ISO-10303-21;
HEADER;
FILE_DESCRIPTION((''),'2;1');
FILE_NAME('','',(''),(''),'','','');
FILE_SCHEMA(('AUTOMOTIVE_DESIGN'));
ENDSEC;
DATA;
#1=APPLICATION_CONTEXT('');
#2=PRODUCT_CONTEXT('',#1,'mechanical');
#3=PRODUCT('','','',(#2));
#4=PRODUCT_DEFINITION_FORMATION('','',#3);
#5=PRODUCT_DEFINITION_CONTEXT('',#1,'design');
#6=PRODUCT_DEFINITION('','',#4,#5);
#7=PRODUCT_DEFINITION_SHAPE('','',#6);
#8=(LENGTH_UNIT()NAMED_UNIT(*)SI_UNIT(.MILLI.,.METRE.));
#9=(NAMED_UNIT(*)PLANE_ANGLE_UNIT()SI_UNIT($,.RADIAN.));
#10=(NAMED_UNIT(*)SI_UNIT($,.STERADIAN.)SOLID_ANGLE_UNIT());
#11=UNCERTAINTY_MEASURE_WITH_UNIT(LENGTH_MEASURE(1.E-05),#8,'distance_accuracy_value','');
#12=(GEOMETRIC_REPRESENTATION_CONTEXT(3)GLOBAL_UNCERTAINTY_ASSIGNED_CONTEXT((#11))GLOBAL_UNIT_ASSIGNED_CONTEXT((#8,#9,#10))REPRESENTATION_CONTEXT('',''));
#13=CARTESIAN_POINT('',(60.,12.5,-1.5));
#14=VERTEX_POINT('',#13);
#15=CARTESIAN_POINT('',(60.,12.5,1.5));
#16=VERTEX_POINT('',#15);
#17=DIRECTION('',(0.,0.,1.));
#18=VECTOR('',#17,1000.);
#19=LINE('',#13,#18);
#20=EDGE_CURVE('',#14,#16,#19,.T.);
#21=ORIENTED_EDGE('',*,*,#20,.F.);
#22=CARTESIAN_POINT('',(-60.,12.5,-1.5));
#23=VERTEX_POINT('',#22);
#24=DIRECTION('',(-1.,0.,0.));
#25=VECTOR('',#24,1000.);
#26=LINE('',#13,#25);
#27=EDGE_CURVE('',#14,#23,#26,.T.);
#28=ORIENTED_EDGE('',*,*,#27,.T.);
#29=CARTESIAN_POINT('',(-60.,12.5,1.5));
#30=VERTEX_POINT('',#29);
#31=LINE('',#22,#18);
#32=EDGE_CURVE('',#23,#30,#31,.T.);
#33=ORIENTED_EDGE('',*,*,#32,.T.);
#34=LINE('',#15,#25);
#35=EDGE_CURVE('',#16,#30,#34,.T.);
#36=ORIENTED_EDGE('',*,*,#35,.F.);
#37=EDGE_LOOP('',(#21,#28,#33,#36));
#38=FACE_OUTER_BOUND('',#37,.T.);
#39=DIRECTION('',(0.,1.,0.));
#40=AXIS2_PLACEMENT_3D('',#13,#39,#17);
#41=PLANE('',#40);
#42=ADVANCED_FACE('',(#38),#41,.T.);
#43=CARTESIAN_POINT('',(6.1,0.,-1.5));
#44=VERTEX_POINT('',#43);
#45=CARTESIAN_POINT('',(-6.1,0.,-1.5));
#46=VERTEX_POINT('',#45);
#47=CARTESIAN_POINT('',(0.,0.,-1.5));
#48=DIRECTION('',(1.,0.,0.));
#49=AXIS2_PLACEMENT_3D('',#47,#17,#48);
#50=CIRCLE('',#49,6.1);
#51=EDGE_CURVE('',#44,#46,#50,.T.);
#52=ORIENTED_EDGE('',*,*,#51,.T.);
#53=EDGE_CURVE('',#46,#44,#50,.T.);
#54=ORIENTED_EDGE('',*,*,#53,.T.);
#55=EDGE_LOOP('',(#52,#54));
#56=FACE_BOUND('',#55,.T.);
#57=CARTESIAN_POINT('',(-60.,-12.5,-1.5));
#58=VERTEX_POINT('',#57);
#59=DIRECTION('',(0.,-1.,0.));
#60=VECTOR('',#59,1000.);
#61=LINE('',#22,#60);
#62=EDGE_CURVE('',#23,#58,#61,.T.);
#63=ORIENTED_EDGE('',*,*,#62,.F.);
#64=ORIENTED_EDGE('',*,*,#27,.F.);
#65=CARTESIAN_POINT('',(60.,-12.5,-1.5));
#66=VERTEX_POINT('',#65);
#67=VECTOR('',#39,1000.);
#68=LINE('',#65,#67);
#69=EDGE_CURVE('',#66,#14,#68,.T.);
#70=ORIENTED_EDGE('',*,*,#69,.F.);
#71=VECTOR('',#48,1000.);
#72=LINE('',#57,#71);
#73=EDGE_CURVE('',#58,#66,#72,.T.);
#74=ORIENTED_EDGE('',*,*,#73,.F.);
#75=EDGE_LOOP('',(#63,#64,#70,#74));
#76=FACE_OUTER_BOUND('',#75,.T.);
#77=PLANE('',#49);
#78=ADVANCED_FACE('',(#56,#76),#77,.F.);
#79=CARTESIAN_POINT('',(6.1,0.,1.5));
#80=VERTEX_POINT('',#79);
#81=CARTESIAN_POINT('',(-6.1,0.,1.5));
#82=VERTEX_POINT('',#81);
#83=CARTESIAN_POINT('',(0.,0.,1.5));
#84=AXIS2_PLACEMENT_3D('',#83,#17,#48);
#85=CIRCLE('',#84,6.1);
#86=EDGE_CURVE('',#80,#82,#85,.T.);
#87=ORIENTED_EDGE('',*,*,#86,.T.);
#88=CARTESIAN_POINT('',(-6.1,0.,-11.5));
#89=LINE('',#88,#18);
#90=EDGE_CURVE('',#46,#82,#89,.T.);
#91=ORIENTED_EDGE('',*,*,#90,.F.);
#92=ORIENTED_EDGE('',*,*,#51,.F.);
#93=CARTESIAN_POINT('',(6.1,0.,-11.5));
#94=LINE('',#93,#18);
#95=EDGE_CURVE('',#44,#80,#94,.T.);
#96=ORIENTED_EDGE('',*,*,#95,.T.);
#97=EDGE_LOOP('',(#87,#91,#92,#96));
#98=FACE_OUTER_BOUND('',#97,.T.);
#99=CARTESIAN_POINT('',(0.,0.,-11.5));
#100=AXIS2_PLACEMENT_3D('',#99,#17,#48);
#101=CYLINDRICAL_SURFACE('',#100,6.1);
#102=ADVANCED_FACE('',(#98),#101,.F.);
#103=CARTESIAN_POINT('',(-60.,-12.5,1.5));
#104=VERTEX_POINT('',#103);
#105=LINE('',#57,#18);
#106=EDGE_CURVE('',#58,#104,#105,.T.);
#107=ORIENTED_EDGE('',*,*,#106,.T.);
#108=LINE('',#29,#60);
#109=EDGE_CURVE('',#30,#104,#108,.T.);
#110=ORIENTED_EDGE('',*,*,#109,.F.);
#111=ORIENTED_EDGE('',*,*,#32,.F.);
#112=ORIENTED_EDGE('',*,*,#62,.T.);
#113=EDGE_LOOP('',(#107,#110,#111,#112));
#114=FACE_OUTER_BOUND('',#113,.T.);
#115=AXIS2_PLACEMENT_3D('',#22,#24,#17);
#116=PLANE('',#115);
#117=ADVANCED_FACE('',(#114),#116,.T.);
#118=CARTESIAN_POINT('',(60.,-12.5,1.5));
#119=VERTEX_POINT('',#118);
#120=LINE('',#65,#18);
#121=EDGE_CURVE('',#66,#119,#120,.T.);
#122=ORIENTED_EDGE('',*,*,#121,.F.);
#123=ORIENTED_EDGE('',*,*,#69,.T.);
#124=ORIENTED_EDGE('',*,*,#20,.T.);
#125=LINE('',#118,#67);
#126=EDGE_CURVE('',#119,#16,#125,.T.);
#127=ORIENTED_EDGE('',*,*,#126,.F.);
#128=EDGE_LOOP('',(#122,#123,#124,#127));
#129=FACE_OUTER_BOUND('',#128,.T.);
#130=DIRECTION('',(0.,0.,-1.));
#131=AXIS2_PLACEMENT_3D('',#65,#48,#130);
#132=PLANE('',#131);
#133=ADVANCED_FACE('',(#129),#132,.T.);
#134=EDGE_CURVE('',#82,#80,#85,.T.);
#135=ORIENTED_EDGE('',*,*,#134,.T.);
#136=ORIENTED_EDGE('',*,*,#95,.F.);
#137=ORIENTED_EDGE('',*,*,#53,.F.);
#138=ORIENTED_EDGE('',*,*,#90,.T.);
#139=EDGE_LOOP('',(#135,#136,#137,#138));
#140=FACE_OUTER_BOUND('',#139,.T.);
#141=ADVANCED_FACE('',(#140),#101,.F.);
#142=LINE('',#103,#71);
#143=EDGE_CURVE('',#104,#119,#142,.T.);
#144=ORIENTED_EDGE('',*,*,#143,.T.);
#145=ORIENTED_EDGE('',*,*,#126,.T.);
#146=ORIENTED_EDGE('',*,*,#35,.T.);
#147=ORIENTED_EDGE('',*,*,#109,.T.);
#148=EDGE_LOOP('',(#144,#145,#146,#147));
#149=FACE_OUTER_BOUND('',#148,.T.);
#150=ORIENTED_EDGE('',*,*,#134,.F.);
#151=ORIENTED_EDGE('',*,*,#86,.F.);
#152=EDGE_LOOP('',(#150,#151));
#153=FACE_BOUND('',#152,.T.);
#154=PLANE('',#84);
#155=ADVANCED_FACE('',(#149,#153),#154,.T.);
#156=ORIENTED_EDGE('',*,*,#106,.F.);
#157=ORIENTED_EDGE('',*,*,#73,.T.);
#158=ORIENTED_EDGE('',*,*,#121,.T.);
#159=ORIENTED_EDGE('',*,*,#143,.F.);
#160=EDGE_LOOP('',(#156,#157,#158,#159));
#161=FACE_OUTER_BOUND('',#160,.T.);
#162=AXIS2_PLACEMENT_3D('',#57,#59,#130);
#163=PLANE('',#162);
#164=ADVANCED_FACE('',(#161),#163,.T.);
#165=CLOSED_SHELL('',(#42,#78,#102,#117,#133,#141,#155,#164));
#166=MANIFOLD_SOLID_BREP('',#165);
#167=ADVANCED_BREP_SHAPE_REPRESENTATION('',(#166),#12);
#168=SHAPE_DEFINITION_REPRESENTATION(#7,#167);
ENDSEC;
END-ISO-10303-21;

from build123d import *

# Parameters (mm, degrees)
SKETCH_1_W          = 120
SKETCH_1_H          = 25
EXTRUDE_1_DEPTH     = 1.5
SKETCH_2_R          = 6.1
CUT_EXTRUDE_1_DEPTH = 11.5


with BuildPart() as part:
    # 草图1 → 凸台-拉伸1 (new, symmetric)
    with BuildSketch(Plane.XY):
        Rectangle(SKETCH_1_W, SKETCH_1_H)
    extrude(amount=EXTRUDE_1_DEPTH, both=True)

    # 草图2 → 切除-拉伸1 (cut, symmetric)
    with BuildSketch(Plane.XY):
        Circle(SKETCH_2_R)
    extrude(amount=CUT_EXTRUDE_1_DEPTH, both=True, mode=Mode.SUBTRACT)


solid = part.part
